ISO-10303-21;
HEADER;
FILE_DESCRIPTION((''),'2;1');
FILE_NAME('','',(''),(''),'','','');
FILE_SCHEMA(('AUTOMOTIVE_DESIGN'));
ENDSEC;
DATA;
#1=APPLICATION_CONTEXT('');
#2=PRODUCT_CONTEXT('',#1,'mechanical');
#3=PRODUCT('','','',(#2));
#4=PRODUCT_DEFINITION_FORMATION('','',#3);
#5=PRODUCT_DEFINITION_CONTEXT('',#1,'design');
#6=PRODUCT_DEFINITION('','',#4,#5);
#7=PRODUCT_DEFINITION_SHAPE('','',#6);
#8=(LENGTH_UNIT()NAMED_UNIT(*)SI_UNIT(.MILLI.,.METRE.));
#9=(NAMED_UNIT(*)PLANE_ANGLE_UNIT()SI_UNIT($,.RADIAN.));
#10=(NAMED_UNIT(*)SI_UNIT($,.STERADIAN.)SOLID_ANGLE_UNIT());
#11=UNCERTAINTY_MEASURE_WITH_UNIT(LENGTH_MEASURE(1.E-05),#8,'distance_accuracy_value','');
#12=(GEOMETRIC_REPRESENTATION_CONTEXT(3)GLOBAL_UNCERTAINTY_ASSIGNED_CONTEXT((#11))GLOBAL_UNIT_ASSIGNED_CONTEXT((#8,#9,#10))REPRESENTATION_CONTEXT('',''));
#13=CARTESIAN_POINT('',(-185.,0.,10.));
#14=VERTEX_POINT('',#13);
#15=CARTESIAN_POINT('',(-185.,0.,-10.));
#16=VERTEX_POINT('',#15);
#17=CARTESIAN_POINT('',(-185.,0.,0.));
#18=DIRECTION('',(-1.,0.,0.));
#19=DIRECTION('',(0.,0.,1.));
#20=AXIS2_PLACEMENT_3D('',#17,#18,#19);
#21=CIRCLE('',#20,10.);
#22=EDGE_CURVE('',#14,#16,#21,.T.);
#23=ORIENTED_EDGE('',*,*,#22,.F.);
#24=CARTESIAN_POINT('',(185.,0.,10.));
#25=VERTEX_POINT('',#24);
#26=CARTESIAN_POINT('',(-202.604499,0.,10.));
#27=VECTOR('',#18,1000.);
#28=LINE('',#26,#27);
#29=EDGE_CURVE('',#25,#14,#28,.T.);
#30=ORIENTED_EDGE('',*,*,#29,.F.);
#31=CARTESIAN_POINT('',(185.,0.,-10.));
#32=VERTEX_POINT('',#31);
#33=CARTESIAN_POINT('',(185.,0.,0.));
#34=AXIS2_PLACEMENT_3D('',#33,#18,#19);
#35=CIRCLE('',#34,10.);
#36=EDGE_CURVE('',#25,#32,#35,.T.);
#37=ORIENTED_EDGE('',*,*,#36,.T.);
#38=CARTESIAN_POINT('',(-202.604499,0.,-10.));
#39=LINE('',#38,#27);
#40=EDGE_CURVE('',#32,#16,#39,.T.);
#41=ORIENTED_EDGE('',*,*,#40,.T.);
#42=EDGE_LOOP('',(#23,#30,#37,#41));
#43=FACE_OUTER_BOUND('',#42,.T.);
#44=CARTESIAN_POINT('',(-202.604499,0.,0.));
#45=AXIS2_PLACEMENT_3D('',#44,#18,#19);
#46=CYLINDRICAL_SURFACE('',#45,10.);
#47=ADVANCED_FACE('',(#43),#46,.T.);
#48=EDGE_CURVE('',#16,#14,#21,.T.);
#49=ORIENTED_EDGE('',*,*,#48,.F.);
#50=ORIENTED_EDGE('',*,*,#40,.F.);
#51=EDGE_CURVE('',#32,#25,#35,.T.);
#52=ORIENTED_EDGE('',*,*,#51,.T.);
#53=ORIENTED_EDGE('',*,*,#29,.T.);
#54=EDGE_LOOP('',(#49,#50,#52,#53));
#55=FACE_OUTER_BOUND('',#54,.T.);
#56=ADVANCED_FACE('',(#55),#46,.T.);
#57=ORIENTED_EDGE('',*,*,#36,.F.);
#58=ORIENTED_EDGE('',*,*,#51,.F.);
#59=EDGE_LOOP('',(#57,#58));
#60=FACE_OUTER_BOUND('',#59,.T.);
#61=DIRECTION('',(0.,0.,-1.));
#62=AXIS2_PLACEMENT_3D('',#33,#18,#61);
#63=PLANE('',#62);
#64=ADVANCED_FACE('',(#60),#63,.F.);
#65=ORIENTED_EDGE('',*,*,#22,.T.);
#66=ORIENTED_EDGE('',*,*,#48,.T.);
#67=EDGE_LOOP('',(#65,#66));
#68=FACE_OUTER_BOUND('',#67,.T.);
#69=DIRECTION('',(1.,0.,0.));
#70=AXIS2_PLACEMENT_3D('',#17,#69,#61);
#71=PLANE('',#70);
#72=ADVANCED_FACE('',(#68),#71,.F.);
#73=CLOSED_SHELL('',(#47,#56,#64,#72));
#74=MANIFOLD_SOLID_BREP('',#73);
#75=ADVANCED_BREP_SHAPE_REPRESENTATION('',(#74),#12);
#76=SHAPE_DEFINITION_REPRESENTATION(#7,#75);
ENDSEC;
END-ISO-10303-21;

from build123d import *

# Parameters (mm, degrees)
SKETCH1_W = 185
SKETCH1_H = 10


with BuildPart() as part:
    # Sketch1 → Revolve1 (revolve)
    with BuildSketch(Plane.XY, mode=Mode.PRIVATE) as revolve1_sk:
        with Locations((-92.5, 5)):
            Rectangle(SKETCH1_W, SKETCH1_H)
    revolve1 = revolve(revolve1_sk.sketch.rotate(Axis((-202.604499093, 0, 0), (1, 0, 0)), 90), axis=Axis((-202.604499093, 0, 0), (1, 0, 0)))

    # Mirror1: Revolve1 across plane
    add(revolve1.mirror(Plane(origin=(0, 0, 0), x_dir=(0, 0, 1), z_dir=(1, 0, 0))))


solid = part.part
